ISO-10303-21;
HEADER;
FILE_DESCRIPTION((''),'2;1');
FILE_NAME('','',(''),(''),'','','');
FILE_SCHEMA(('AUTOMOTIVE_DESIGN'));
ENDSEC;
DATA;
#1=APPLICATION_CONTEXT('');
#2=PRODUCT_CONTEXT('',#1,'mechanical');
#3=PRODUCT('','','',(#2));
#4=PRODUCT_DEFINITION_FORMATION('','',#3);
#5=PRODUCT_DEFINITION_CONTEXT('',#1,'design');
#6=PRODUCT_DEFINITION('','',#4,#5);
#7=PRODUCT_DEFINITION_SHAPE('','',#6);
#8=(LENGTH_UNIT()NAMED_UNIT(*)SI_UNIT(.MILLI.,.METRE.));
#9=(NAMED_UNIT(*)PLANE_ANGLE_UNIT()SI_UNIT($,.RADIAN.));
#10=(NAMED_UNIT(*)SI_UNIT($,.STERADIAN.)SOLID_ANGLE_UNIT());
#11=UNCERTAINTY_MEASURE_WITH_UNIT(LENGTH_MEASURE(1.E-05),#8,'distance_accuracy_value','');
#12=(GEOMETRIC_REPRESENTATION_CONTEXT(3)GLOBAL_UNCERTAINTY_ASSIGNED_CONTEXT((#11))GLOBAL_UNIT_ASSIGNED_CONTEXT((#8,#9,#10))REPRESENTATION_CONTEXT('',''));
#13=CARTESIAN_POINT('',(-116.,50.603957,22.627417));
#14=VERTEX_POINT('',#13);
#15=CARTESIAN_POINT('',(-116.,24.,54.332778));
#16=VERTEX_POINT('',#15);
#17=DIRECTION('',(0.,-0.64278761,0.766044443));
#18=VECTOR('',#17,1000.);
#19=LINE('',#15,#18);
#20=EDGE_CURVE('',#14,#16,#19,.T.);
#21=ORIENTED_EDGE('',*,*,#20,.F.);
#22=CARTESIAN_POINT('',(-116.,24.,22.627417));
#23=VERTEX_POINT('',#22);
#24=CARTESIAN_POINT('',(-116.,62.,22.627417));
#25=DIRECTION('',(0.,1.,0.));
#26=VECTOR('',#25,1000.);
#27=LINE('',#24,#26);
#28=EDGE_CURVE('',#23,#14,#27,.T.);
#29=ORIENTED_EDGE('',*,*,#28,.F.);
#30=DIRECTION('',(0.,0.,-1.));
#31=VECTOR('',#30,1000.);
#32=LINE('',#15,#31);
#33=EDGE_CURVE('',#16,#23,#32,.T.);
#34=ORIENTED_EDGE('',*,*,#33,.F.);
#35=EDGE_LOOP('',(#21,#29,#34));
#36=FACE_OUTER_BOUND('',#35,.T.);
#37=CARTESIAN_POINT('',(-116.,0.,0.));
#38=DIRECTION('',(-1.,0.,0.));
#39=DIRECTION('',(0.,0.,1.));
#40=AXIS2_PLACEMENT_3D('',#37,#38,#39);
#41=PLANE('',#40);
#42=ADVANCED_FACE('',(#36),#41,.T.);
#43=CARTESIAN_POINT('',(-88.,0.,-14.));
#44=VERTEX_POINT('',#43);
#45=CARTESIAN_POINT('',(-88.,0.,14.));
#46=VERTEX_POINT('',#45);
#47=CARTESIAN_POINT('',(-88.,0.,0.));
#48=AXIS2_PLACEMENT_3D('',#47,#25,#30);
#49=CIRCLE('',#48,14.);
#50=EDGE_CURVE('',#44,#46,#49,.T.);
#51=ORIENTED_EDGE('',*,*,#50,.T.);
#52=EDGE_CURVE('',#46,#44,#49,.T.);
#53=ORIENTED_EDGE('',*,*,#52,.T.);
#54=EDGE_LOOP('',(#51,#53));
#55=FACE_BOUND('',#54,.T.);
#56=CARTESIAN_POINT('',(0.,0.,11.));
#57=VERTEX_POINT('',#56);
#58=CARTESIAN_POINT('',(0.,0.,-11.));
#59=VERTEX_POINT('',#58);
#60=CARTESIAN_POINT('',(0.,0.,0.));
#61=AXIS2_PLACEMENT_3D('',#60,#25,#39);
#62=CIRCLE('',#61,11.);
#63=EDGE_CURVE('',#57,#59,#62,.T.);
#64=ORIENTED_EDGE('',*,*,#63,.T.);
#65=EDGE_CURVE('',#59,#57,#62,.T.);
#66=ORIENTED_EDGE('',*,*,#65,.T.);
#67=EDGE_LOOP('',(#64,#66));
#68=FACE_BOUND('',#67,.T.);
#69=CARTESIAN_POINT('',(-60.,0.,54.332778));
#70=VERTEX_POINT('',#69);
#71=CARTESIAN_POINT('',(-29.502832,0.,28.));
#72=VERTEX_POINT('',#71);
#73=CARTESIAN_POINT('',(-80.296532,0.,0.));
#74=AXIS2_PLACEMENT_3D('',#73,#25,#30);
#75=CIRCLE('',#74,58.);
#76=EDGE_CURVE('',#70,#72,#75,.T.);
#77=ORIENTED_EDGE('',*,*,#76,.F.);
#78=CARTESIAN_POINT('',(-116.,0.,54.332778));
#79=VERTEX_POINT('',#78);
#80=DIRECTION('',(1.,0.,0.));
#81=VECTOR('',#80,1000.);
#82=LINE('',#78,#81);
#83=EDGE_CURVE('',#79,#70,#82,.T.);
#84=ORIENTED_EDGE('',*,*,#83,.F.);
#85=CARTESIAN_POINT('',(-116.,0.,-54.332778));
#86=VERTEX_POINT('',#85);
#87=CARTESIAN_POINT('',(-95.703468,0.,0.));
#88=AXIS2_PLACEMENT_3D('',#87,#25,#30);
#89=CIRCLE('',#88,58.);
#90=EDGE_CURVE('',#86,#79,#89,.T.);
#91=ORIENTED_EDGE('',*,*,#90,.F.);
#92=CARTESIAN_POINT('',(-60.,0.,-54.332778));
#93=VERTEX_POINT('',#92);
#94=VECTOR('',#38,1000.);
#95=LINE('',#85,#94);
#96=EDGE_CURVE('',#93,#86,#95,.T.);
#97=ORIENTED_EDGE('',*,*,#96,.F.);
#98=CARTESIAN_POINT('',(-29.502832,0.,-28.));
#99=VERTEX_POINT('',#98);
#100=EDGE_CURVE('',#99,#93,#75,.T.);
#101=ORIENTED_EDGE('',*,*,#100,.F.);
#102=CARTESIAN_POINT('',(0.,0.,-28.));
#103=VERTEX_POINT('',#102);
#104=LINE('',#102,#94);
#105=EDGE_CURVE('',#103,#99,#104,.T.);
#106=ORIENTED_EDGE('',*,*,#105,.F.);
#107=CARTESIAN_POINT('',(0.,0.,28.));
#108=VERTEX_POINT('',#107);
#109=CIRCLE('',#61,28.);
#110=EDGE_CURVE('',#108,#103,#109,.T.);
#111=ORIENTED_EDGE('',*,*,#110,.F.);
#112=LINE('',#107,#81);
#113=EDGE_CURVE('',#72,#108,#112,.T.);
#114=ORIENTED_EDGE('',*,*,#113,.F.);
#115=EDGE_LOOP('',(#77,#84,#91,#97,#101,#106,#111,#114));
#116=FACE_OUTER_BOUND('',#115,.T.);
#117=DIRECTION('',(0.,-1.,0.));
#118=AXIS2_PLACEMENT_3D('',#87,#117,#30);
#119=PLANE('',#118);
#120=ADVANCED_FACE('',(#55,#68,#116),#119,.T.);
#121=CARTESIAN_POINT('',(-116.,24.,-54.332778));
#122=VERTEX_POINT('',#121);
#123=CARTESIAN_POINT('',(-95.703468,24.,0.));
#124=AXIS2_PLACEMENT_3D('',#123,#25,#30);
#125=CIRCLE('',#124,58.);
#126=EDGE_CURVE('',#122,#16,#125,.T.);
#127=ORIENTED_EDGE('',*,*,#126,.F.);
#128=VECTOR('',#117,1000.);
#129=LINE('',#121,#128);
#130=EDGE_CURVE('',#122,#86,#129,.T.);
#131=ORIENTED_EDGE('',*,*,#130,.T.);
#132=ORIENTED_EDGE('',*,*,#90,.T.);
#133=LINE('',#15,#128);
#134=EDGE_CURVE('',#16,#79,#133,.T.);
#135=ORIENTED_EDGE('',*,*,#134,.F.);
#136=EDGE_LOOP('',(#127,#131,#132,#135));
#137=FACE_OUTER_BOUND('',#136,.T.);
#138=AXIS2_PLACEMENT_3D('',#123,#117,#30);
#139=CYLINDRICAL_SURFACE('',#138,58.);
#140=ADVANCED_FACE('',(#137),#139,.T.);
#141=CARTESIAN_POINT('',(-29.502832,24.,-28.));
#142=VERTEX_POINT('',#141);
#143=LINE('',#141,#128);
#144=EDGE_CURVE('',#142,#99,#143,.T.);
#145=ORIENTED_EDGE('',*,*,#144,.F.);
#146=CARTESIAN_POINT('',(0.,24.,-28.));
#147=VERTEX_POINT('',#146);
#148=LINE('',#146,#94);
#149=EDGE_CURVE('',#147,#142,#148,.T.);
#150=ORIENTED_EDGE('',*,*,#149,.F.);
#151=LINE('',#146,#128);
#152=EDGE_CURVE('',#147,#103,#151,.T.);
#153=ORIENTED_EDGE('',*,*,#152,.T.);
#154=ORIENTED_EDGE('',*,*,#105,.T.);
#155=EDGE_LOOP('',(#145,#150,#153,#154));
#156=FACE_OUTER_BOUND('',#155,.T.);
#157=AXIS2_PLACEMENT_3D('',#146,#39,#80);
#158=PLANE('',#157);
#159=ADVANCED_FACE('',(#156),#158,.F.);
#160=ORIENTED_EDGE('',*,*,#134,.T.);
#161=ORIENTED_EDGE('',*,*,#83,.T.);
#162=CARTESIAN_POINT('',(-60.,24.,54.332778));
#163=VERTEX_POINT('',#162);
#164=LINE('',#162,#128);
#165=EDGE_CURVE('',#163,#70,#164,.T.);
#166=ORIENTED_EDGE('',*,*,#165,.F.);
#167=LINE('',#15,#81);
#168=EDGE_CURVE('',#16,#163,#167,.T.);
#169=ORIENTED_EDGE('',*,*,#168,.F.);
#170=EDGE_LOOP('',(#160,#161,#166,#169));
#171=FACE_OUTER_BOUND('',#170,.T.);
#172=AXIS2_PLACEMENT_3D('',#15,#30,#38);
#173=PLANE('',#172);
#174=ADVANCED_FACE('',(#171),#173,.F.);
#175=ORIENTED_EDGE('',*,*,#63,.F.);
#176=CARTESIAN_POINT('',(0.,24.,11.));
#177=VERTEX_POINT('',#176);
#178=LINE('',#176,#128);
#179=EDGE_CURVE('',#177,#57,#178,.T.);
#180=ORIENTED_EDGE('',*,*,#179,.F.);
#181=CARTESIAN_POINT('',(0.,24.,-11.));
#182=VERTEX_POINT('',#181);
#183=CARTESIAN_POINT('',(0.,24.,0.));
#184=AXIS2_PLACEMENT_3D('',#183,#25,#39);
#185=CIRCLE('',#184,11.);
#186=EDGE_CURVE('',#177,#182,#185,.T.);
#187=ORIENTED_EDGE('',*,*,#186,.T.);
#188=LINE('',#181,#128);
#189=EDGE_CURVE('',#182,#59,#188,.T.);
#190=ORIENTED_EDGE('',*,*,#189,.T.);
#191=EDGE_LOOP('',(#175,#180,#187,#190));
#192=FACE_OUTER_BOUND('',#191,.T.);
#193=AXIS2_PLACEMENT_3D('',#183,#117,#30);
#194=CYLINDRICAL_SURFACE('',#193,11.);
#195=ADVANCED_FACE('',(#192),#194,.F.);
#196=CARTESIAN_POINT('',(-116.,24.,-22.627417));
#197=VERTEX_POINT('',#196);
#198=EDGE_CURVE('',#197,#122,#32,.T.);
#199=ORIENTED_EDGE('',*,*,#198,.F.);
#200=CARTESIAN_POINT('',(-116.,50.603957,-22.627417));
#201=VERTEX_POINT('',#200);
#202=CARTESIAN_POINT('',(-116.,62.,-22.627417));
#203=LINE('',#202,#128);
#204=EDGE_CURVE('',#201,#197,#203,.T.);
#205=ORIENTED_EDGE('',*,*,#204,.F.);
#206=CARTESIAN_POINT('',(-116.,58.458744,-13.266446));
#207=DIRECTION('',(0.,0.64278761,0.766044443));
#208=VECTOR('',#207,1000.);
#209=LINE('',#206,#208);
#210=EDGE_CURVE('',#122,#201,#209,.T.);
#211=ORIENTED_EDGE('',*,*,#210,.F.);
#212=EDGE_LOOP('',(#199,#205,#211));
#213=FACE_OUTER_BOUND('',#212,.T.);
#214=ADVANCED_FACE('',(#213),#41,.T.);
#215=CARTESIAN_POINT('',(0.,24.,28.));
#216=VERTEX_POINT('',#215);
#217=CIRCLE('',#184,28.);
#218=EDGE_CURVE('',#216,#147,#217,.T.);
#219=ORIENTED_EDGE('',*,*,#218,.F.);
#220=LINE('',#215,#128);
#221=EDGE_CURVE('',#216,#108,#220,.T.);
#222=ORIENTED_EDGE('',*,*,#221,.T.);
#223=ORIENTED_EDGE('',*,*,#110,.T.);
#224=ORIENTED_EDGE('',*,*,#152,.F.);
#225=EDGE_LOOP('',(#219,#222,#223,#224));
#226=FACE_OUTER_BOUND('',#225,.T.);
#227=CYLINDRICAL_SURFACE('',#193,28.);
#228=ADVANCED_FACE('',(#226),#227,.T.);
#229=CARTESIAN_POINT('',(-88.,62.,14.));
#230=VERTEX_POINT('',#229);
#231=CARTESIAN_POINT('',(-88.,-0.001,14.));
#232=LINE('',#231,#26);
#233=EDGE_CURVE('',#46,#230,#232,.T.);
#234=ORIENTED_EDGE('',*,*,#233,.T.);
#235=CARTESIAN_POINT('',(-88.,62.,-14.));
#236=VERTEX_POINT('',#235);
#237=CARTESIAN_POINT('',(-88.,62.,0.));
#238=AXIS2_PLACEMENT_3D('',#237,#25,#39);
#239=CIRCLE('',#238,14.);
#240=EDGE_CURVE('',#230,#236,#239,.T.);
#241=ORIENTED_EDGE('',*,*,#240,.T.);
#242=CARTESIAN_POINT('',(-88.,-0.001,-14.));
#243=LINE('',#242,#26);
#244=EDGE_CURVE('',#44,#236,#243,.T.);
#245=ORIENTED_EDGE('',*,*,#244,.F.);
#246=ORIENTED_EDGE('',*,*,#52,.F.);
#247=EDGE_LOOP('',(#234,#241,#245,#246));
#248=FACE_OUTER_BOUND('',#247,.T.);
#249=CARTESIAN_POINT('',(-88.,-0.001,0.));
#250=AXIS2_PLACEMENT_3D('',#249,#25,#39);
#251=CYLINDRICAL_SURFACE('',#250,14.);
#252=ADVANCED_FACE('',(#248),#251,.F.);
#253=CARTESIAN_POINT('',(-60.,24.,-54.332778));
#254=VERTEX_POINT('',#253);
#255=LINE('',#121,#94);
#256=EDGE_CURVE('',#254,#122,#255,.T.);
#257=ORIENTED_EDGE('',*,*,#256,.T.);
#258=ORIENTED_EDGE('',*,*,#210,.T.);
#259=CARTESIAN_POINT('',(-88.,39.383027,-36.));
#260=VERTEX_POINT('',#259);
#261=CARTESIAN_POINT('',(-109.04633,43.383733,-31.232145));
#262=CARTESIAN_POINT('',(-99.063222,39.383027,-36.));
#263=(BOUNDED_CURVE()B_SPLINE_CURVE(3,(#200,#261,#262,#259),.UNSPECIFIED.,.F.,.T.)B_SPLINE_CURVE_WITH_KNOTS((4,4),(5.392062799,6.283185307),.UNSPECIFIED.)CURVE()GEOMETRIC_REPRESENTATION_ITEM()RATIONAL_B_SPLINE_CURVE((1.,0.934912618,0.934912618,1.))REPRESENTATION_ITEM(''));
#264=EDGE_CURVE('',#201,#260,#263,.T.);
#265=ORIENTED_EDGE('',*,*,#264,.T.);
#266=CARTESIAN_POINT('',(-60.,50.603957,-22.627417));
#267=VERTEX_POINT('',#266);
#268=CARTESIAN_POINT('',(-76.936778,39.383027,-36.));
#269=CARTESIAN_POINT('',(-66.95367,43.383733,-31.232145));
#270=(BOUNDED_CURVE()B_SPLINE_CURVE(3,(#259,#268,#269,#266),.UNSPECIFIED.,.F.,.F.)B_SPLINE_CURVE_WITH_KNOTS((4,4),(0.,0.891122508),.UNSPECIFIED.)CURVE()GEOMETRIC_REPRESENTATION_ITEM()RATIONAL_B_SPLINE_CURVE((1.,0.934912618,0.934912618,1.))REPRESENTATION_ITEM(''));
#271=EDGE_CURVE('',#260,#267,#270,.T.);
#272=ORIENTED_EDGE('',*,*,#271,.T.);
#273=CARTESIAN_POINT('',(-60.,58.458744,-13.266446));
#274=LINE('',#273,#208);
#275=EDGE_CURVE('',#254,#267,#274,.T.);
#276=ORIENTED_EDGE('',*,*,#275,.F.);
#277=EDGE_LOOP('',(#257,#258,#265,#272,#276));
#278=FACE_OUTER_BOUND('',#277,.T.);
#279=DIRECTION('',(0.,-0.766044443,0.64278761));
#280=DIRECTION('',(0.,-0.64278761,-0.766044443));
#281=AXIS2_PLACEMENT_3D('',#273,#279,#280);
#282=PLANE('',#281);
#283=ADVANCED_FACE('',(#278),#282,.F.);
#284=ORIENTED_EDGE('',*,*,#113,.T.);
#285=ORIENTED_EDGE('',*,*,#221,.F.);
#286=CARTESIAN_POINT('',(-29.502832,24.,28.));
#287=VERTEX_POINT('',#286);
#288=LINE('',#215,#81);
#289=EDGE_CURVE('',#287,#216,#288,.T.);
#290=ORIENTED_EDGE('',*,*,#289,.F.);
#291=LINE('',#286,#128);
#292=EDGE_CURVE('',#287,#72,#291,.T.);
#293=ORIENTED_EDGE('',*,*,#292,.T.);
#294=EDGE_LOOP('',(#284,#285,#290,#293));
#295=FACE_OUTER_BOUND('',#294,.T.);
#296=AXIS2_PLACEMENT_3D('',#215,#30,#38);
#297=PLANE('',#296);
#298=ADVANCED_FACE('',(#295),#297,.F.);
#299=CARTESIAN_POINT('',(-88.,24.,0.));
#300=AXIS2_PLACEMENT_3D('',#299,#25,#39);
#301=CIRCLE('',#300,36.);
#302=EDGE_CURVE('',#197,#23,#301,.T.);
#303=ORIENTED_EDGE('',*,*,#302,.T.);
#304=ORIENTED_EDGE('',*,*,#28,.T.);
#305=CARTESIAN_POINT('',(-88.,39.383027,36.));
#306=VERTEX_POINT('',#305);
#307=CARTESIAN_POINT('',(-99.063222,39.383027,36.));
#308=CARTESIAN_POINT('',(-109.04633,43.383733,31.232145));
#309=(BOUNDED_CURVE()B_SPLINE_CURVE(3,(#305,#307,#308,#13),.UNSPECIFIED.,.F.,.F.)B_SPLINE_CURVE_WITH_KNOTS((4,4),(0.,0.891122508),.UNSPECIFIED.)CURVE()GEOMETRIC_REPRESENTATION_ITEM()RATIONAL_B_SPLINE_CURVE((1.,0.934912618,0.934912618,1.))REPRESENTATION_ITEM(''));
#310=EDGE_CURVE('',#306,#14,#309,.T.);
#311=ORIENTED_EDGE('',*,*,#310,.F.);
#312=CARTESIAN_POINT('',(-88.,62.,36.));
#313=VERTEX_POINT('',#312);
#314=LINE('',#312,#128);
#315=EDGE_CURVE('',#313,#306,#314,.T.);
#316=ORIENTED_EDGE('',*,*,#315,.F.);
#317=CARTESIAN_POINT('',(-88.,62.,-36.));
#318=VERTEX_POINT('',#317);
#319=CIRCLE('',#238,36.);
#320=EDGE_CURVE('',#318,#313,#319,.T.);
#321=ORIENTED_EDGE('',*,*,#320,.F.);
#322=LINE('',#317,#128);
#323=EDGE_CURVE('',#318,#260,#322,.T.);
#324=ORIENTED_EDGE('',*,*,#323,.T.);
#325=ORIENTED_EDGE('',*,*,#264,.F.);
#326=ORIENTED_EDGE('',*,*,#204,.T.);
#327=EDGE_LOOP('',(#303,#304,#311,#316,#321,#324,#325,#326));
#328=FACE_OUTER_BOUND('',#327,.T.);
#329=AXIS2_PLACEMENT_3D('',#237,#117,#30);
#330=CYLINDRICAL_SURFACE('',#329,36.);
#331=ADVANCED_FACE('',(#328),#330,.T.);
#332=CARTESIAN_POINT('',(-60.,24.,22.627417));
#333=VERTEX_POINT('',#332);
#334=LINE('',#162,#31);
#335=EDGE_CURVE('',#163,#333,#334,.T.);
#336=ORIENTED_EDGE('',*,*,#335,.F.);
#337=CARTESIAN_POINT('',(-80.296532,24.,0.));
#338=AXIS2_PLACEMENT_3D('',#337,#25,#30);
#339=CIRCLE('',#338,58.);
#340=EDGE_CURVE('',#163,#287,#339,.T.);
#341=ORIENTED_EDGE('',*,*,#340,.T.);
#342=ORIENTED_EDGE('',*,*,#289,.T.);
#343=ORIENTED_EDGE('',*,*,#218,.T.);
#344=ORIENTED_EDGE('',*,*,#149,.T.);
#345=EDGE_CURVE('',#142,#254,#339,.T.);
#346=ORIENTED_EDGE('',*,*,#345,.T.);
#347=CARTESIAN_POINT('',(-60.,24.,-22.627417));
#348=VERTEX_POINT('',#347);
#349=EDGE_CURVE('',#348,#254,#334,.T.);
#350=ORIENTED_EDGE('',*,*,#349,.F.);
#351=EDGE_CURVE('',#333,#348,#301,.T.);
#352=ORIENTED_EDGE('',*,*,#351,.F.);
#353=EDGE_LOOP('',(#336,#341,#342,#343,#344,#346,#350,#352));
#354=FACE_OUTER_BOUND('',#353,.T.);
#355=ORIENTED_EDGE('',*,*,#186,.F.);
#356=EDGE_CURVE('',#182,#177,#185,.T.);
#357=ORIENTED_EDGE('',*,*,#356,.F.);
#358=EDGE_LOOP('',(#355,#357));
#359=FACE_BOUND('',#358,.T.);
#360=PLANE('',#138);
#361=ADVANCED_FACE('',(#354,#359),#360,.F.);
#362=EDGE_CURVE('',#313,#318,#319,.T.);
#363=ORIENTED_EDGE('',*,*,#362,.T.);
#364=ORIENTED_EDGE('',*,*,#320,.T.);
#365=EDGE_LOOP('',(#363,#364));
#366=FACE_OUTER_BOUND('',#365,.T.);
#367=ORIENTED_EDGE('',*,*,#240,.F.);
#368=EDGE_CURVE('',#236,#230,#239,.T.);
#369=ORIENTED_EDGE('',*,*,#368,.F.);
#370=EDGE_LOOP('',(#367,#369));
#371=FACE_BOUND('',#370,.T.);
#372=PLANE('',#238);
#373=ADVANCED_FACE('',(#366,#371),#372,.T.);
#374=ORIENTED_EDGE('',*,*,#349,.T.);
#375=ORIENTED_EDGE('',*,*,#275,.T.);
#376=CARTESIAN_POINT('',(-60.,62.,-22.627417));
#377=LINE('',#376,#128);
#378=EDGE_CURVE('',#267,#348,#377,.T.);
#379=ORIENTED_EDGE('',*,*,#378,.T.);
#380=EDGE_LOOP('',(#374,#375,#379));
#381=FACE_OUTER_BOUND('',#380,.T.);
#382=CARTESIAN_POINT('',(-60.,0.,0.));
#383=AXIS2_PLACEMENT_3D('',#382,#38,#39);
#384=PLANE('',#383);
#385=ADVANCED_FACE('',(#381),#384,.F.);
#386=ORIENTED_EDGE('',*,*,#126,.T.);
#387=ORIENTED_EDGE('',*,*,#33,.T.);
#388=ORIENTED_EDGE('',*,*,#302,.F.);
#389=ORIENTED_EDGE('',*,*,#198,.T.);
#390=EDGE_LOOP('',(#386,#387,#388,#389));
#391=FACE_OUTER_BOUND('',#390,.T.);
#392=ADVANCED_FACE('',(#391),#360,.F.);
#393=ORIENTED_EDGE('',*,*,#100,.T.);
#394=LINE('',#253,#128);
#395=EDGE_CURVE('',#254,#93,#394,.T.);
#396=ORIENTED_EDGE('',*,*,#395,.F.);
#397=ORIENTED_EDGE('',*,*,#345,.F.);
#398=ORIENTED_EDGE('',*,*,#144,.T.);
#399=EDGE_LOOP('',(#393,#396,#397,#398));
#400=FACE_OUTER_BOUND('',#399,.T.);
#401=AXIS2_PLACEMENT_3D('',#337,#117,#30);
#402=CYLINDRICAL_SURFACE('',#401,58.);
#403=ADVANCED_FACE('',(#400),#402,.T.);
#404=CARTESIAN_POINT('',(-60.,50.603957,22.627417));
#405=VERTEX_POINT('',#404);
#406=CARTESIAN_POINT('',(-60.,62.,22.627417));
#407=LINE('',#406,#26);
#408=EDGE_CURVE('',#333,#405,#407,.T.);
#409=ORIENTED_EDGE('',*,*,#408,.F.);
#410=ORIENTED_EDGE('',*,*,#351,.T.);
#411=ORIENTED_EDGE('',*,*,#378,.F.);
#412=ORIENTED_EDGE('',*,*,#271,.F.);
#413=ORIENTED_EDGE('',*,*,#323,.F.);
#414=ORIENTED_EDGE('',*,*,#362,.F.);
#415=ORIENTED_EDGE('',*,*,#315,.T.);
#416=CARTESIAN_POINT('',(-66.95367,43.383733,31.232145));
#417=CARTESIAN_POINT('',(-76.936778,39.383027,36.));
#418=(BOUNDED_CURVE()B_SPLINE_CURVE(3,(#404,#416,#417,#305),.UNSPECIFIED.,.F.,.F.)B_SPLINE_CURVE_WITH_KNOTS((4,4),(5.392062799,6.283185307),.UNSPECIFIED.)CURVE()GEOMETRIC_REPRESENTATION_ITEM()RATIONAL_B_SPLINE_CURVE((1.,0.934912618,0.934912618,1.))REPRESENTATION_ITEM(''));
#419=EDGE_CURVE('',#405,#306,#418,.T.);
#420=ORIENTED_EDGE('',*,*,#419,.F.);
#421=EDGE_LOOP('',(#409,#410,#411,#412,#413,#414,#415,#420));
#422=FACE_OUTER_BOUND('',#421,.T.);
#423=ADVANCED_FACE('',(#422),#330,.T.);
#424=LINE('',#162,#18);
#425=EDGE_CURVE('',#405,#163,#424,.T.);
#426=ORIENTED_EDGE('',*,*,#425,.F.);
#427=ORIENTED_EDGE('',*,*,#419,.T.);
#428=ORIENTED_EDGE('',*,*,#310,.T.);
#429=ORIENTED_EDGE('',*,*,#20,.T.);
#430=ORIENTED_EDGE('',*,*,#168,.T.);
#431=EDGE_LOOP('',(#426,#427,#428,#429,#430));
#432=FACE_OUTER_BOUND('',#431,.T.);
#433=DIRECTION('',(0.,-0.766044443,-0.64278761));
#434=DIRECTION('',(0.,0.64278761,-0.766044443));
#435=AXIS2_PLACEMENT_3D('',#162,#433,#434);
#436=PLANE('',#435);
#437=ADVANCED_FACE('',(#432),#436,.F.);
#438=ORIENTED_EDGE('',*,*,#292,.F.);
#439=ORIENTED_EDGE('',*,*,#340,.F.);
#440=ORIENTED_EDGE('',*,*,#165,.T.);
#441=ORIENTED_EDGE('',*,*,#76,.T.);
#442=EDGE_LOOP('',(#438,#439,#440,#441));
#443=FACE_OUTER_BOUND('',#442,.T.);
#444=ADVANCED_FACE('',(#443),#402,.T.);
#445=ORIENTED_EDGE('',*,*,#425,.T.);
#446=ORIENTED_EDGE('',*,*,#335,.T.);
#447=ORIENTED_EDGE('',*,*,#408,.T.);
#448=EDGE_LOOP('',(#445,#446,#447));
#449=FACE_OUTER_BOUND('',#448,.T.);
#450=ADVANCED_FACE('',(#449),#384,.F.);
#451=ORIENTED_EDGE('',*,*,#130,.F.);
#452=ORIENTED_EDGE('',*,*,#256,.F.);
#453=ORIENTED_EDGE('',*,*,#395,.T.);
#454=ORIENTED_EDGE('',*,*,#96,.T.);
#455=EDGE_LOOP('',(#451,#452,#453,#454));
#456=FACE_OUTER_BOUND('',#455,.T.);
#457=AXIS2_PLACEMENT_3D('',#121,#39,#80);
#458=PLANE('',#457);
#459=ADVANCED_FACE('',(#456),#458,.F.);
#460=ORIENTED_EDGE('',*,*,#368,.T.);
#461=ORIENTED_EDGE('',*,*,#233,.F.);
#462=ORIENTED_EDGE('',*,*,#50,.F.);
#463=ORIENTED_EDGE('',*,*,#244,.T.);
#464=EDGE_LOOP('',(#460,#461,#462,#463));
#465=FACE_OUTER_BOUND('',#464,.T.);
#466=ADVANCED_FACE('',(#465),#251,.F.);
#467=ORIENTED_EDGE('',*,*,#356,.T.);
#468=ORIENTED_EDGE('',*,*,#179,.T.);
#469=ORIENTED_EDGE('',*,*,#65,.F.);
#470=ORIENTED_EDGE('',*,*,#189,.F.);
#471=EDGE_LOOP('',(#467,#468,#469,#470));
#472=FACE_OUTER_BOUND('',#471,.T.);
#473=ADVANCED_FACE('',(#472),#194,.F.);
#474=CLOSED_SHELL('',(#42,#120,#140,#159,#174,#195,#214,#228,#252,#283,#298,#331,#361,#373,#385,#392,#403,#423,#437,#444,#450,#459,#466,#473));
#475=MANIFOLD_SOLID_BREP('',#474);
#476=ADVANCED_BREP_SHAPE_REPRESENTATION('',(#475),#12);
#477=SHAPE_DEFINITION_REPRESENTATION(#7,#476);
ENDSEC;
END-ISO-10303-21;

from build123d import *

# Parameters (mm, degrees)
BASE_FLANGE_SKETCH_R = 11
BASE_FLANGE_DEPTH    = 24
HUB_BOSS_SKETCH_72_R = 36
HUB_BOSS_72_DEPTH    = 38
WEDGE_SUPPORT_DEPTH  = 28
BORE_28_REACH        = 176.416
BORE_SKETCH_28_R     = 14


with BuildPart() as part:
    # Base Flange Sketch → Base Flange (new body)
    with BuildSketch(Plane(origin=(0, 0, 0), x_dir=(1, 0, 0), z_dir=(0, 1, 0))):
        with BuildLine():
            Line((-116, 54.332778116), (-60, 54.332778116))
            ThreePointArc((-60, 54.332778116), (-42.391267518, 43.899782505), (-29.502831874, 28))
            Line((-29.502831874, 28), (0, 28))
            ThreePointArc((0, 28), (28, 0), (0, -28))
            Line((0, -28), (-29.502831874, -28))
            ThreePointArc((-29.502831874, -28), (-42.391267518, -43.899782505), (-60, -54.332778116))
            Line((-60, -54.332778116), (-116, -54.332778116))
            ThreePointArc((-116, -54.332778116), (-153.703467729, 0), (-116, 54.332778116))
        make_face()
        with Locations(Location((0, 0, 0), (0, 0, 270))):
            Circle(BASE_FLANGE_SKETCH_R, mode=Mode.SUBTRACT)
    extrude(amount=BASE_FLANGE_DEPTH)

    # Hub Boss Sketch Ø72 → Hub Boss Ø72 (add)
    with BuildSketch(Plane(origin=(0, 24, 0), x_dir=(1, 0, 0), z_dir=(0, 1, 0))):
        with Locations(Location((-88, 0, 0), (0, 0, 270))):
            Circle(HUB_BOSS_SKETCH_72_R)
    extrude(amount=HUB_BOSS_72_DEPTH)

    # Wedge Support Sketch → Wedge Support (add, symmetric)
    with BuildSketch(Plane(origin=(-88, 0, 0), x_dir=(0, 0, -1), z_dir=(1, 0, 0))):
        Polygon((-54.332778116, 24), (-13.504322415, 58.25914212), (13.266446181, 58.45874398), (54.332778116, 24), align=None)
    extrude(amount=WEDGE_SUPPORT_DEPTH, both=True)

    # Bore Sketch Ø28 → Bore Ø28 (cut, up to next)
    with BuildSketch(Plane(origin=(0, 62, 0), x_dir=(1, 0, 0), z_dir=(0, 1, 0)), mode=Mode.PRIVATE) as bore_28_sk1:
        with Locations(Location((-88, 0, 0), (0, 0, 270))):
            Circle(BORE_SKETCH_28_R)
    bore_28_tool1 = extrude(bore_28_sk1.sketch, amount=-BORE_28_REACH, mode=Mode.PRIVATE) & part.part
    add(bore_28_tool1.solids().sort_by_distance((-88, 62, 0))[0], mode=Mode.SUBTRACT)


solid = part.part
